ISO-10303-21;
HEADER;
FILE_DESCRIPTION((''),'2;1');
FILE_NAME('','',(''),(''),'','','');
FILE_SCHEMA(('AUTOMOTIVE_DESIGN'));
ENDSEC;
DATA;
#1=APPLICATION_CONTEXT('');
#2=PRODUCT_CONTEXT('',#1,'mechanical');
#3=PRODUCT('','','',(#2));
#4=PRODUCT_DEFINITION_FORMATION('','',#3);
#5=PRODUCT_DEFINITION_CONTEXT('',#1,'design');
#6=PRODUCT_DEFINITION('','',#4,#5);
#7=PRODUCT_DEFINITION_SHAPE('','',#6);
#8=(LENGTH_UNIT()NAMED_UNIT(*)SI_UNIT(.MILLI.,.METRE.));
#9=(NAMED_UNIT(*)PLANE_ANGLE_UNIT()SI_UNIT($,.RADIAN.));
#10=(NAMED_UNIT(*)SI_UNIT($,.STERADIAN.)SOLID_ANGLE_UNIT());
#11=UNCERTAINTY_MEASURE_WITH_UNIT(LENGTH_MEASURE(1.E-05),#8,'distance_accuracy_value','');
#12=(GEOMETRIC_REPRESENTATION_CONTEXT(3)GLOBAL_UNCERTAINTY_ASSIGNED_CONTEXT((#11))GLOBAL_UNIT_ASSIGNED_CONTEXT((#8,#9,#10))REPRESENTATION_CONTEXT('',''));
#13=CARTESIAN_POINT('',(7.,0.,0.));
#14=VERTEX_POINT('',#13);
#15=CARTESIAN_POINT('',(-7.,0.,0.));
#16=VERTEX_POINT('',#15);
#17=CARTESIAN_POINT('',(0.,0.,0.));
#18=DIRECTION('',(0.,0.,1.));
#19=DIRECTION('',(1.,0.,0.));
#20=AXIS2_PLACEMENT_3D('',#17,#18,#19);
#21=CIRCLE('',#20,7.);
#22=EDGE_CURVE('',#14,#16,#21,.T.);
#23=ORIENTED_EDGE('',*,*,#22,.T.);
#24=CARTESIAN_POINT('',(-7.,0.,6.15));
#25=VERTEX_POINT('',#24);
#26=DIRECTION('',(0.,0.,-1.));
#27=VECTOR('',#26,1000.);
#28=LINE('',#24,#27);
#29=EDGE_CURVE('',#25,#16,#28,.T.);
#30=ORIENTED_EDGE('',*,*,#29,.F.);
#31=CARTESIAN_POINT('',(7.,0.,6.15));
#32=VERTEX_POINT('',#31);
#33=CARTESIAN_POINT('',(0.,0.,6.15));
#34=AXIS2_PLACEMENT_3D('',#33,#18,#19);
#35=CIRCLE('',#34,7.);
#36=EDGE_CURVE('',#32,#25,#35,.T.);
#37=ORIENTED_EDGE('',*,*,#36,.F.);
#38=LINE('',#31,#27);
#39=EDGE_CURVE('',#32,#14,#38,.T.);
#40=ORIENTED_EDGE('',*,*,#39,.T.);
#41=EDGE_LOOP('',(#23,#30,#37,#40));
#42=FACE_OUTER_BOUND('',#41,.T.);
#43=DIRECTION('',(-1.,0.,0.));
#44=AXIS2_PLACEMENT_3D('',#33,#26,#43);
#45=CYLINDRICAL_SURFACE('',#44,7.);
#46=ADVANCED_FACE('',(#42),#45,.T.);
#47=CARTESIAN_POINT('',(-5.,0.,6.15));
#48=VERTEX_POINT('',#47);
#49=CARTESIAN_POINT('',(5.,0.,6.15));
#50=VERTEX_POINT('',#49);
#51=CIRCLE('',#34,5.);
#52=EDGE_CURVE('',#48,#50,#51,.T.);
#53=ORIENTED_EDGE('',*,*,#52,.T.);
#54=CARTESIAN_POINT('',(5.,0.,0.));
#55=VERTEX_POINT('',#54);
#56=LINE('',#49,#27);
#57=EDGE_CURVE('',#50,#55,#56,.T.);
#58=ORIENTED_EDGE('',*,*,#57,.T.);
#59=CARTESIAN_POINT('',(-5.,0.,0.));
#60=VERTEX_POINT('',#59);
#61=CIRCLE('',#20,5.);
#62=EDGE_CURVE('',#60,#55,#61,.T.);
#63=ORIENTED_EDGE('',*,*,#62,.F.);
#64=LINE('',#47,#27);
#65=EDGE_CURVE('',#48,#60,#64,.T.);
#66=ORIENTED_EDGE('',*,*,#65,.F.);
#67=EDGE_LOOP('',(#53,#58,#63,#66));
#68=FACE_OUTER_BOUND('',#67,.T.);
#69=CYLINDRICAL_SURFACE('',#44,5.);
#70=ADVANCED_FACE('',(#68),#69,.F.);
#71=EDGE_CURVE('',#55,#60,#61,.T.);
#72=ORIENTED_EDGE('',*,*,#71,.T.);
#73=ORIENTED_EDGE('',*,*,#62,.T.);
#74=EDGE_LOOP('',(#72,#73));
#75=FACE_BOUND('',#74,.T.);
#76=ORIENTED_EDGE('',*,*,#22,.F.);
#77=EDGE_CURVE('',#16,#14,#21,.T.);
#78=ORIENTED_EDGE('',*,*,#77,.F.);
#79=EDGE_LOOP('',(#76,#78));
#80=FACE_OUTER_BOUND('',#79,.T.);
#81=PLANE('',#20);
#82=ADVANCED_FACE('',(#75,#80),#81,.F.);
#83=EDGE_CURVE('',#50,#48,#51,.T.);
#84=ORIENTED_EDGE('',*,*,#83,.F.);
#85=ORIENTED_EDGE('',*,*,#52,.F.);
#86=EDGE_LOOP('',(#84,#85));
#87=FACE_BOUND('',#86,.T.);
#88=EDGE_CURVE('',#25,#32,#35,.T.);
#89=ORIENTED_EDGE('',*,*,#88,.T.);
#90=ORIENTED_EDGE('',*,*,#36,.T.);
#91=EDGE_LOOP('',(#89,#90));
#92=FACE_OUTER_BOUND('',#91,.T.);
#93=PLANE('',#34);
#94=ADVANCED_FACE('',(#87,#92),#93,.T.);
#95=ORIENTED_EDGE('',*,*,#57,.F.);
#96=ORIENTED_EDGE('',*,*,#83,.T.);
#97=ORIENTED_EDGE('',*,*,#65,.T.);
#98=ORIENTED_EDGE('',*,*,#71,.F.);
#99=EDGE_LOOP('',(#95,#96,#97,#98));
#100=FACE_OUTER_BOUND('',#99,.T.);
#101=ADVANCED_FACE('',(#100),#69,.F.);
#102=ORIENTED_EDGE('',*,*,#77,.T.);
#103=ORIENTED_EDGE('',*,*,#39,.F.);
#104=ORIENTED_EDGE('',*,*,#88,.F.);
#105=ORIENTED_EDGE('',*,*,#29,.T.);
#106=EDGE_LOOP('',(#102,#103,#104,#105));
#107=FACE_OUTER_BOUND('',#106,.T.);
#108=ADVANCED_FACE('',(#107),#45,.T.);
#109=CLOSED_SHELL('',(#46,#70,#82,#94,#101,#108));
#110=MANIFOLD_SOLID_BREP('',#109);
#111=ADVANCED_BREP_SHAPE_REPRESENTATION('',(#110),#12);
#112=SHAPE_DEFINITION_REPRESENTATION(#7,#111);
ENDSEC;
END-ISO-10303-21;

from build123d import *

# Parameters (mm, degrees)
SKETCH_1_R      = 7
SKETCH_1_R_2    = 5
EXTRUDE_1_DEPTH = 6.15


with BuildPart() as part:
    # 草图1 → 凸台-拉伸1 (new body)
    with BuildSketch(Plane.XY):
        Circle(SKETCH_1_R)
        Circle(SKETCH_1_R_2, mode=Mode.SUBTRACT)
    extrude(amount=EXTRUDE_1_DEPTH)


solid = part.part
